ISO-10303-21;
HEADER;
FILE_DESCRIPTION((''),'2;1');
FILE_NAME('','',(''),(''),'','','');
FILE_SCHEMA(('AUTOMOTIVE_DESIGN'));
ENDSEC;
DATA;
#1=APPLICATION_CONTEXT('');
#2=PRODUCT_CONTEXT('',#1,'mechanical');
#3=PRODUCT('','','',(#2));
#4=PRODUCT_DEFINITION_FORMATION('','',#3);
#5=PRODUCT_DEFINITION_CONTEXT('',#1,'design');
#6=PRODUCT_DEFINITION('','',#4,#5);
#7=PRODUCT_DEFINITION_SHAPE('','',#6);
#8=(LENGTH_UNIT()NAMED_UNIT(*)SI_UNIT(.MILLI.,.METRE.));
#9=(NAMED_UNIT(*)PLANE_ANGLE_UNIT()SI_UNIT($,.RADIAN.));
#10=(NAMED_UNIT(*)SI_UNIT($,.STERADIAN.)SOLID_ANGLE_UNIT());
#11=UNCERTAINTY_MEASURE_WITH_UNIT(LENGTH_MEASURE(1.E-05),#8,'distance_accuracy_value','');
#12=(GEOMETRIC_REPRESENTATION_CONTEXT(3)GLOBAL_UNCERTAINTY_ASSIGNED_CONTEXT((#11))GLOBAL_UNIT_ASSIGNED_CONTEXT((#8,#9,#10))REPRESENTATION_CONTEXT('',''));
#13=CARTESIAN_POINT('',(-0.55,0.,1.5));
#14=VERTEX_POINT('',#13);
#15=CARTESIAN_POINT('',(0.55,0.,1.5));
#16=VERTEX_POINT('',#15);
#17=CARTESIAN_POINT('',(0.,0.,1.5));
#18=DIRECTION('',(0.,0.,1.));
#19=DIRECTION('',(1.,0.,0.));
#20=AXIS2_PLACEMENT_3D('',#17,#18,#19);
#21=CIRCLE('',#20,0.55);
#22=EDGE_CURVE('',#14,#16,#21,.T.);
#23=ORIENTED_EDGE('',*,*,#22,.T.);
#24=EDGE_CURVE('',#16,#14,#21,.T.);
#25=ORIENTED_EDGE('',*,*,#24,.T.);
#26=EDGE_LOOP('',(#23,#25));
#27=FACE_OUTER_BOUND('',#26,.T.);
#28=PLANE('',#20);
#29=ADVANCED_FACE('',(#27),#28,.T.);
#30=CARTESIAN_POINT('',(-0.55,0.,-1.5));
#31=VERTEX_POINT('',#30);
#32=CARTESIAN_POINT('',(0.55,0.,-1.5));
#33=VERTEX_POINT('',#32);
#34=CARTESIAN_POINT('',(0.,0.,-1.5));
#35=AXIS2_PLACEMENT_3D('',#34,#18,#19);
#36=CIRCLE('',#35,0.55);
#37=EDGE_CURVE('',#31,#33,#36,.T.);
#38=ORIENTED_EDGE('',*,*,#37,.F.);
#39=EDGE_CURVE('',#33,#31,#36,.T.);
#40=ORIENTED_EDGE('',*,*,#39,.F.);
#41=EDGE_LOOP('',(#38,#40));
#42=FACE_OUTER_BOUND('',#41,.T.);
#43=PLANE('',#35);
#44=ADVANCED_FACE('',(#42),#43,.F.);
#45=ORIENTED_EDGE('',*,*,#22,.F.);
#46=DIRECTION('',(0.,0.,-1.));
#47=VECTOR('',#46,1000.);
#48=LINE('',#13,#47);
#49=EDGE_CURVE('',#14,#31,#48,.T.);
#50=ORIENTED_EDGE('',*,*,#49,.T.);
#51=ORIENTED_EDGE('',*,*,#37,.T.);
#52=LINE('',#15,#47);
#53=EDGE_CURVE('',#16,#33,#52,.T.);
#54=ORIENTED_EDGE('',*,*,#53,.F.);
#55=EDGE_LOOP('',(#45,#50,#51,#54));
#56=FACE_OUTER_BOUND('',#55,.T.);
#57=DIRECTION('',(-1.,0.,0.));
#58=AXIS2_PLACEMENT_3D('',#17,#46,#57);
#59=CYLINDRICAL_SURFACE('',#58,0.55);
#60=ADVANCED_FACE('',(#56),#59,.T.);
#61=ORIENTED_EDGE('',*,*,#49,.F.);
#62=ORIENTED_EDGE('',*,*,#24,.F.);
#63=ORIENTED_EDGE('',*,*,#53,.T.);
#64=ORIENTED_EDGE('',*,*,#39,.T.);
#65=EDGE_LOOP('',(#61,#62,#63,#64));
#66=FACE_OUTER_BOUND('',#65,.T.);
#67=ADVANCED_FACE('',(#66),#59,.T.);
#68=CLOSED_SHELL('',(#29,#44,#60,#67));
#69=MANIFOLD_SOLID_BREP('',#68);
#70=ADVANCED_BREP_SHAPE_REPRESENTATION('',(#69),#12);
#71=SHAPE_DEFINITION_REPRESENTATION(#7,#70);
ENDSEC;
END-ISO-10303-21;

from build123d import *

# Parameters (mm, degrees)
SKETCH1_R           = 0.55
BOSS_EXTRUDE1_DEPTH = 1.5


with BuildPart() as part:
    # Sketch1 → Boss-Extrude1 (new, symmetric)
    with BuildSketch(Plane.XY):
        Circle(SKETCH1_R)
    extrude(amount=BOSS_EXTRUDE1_DEPTH, both=True)


solid = part.part
